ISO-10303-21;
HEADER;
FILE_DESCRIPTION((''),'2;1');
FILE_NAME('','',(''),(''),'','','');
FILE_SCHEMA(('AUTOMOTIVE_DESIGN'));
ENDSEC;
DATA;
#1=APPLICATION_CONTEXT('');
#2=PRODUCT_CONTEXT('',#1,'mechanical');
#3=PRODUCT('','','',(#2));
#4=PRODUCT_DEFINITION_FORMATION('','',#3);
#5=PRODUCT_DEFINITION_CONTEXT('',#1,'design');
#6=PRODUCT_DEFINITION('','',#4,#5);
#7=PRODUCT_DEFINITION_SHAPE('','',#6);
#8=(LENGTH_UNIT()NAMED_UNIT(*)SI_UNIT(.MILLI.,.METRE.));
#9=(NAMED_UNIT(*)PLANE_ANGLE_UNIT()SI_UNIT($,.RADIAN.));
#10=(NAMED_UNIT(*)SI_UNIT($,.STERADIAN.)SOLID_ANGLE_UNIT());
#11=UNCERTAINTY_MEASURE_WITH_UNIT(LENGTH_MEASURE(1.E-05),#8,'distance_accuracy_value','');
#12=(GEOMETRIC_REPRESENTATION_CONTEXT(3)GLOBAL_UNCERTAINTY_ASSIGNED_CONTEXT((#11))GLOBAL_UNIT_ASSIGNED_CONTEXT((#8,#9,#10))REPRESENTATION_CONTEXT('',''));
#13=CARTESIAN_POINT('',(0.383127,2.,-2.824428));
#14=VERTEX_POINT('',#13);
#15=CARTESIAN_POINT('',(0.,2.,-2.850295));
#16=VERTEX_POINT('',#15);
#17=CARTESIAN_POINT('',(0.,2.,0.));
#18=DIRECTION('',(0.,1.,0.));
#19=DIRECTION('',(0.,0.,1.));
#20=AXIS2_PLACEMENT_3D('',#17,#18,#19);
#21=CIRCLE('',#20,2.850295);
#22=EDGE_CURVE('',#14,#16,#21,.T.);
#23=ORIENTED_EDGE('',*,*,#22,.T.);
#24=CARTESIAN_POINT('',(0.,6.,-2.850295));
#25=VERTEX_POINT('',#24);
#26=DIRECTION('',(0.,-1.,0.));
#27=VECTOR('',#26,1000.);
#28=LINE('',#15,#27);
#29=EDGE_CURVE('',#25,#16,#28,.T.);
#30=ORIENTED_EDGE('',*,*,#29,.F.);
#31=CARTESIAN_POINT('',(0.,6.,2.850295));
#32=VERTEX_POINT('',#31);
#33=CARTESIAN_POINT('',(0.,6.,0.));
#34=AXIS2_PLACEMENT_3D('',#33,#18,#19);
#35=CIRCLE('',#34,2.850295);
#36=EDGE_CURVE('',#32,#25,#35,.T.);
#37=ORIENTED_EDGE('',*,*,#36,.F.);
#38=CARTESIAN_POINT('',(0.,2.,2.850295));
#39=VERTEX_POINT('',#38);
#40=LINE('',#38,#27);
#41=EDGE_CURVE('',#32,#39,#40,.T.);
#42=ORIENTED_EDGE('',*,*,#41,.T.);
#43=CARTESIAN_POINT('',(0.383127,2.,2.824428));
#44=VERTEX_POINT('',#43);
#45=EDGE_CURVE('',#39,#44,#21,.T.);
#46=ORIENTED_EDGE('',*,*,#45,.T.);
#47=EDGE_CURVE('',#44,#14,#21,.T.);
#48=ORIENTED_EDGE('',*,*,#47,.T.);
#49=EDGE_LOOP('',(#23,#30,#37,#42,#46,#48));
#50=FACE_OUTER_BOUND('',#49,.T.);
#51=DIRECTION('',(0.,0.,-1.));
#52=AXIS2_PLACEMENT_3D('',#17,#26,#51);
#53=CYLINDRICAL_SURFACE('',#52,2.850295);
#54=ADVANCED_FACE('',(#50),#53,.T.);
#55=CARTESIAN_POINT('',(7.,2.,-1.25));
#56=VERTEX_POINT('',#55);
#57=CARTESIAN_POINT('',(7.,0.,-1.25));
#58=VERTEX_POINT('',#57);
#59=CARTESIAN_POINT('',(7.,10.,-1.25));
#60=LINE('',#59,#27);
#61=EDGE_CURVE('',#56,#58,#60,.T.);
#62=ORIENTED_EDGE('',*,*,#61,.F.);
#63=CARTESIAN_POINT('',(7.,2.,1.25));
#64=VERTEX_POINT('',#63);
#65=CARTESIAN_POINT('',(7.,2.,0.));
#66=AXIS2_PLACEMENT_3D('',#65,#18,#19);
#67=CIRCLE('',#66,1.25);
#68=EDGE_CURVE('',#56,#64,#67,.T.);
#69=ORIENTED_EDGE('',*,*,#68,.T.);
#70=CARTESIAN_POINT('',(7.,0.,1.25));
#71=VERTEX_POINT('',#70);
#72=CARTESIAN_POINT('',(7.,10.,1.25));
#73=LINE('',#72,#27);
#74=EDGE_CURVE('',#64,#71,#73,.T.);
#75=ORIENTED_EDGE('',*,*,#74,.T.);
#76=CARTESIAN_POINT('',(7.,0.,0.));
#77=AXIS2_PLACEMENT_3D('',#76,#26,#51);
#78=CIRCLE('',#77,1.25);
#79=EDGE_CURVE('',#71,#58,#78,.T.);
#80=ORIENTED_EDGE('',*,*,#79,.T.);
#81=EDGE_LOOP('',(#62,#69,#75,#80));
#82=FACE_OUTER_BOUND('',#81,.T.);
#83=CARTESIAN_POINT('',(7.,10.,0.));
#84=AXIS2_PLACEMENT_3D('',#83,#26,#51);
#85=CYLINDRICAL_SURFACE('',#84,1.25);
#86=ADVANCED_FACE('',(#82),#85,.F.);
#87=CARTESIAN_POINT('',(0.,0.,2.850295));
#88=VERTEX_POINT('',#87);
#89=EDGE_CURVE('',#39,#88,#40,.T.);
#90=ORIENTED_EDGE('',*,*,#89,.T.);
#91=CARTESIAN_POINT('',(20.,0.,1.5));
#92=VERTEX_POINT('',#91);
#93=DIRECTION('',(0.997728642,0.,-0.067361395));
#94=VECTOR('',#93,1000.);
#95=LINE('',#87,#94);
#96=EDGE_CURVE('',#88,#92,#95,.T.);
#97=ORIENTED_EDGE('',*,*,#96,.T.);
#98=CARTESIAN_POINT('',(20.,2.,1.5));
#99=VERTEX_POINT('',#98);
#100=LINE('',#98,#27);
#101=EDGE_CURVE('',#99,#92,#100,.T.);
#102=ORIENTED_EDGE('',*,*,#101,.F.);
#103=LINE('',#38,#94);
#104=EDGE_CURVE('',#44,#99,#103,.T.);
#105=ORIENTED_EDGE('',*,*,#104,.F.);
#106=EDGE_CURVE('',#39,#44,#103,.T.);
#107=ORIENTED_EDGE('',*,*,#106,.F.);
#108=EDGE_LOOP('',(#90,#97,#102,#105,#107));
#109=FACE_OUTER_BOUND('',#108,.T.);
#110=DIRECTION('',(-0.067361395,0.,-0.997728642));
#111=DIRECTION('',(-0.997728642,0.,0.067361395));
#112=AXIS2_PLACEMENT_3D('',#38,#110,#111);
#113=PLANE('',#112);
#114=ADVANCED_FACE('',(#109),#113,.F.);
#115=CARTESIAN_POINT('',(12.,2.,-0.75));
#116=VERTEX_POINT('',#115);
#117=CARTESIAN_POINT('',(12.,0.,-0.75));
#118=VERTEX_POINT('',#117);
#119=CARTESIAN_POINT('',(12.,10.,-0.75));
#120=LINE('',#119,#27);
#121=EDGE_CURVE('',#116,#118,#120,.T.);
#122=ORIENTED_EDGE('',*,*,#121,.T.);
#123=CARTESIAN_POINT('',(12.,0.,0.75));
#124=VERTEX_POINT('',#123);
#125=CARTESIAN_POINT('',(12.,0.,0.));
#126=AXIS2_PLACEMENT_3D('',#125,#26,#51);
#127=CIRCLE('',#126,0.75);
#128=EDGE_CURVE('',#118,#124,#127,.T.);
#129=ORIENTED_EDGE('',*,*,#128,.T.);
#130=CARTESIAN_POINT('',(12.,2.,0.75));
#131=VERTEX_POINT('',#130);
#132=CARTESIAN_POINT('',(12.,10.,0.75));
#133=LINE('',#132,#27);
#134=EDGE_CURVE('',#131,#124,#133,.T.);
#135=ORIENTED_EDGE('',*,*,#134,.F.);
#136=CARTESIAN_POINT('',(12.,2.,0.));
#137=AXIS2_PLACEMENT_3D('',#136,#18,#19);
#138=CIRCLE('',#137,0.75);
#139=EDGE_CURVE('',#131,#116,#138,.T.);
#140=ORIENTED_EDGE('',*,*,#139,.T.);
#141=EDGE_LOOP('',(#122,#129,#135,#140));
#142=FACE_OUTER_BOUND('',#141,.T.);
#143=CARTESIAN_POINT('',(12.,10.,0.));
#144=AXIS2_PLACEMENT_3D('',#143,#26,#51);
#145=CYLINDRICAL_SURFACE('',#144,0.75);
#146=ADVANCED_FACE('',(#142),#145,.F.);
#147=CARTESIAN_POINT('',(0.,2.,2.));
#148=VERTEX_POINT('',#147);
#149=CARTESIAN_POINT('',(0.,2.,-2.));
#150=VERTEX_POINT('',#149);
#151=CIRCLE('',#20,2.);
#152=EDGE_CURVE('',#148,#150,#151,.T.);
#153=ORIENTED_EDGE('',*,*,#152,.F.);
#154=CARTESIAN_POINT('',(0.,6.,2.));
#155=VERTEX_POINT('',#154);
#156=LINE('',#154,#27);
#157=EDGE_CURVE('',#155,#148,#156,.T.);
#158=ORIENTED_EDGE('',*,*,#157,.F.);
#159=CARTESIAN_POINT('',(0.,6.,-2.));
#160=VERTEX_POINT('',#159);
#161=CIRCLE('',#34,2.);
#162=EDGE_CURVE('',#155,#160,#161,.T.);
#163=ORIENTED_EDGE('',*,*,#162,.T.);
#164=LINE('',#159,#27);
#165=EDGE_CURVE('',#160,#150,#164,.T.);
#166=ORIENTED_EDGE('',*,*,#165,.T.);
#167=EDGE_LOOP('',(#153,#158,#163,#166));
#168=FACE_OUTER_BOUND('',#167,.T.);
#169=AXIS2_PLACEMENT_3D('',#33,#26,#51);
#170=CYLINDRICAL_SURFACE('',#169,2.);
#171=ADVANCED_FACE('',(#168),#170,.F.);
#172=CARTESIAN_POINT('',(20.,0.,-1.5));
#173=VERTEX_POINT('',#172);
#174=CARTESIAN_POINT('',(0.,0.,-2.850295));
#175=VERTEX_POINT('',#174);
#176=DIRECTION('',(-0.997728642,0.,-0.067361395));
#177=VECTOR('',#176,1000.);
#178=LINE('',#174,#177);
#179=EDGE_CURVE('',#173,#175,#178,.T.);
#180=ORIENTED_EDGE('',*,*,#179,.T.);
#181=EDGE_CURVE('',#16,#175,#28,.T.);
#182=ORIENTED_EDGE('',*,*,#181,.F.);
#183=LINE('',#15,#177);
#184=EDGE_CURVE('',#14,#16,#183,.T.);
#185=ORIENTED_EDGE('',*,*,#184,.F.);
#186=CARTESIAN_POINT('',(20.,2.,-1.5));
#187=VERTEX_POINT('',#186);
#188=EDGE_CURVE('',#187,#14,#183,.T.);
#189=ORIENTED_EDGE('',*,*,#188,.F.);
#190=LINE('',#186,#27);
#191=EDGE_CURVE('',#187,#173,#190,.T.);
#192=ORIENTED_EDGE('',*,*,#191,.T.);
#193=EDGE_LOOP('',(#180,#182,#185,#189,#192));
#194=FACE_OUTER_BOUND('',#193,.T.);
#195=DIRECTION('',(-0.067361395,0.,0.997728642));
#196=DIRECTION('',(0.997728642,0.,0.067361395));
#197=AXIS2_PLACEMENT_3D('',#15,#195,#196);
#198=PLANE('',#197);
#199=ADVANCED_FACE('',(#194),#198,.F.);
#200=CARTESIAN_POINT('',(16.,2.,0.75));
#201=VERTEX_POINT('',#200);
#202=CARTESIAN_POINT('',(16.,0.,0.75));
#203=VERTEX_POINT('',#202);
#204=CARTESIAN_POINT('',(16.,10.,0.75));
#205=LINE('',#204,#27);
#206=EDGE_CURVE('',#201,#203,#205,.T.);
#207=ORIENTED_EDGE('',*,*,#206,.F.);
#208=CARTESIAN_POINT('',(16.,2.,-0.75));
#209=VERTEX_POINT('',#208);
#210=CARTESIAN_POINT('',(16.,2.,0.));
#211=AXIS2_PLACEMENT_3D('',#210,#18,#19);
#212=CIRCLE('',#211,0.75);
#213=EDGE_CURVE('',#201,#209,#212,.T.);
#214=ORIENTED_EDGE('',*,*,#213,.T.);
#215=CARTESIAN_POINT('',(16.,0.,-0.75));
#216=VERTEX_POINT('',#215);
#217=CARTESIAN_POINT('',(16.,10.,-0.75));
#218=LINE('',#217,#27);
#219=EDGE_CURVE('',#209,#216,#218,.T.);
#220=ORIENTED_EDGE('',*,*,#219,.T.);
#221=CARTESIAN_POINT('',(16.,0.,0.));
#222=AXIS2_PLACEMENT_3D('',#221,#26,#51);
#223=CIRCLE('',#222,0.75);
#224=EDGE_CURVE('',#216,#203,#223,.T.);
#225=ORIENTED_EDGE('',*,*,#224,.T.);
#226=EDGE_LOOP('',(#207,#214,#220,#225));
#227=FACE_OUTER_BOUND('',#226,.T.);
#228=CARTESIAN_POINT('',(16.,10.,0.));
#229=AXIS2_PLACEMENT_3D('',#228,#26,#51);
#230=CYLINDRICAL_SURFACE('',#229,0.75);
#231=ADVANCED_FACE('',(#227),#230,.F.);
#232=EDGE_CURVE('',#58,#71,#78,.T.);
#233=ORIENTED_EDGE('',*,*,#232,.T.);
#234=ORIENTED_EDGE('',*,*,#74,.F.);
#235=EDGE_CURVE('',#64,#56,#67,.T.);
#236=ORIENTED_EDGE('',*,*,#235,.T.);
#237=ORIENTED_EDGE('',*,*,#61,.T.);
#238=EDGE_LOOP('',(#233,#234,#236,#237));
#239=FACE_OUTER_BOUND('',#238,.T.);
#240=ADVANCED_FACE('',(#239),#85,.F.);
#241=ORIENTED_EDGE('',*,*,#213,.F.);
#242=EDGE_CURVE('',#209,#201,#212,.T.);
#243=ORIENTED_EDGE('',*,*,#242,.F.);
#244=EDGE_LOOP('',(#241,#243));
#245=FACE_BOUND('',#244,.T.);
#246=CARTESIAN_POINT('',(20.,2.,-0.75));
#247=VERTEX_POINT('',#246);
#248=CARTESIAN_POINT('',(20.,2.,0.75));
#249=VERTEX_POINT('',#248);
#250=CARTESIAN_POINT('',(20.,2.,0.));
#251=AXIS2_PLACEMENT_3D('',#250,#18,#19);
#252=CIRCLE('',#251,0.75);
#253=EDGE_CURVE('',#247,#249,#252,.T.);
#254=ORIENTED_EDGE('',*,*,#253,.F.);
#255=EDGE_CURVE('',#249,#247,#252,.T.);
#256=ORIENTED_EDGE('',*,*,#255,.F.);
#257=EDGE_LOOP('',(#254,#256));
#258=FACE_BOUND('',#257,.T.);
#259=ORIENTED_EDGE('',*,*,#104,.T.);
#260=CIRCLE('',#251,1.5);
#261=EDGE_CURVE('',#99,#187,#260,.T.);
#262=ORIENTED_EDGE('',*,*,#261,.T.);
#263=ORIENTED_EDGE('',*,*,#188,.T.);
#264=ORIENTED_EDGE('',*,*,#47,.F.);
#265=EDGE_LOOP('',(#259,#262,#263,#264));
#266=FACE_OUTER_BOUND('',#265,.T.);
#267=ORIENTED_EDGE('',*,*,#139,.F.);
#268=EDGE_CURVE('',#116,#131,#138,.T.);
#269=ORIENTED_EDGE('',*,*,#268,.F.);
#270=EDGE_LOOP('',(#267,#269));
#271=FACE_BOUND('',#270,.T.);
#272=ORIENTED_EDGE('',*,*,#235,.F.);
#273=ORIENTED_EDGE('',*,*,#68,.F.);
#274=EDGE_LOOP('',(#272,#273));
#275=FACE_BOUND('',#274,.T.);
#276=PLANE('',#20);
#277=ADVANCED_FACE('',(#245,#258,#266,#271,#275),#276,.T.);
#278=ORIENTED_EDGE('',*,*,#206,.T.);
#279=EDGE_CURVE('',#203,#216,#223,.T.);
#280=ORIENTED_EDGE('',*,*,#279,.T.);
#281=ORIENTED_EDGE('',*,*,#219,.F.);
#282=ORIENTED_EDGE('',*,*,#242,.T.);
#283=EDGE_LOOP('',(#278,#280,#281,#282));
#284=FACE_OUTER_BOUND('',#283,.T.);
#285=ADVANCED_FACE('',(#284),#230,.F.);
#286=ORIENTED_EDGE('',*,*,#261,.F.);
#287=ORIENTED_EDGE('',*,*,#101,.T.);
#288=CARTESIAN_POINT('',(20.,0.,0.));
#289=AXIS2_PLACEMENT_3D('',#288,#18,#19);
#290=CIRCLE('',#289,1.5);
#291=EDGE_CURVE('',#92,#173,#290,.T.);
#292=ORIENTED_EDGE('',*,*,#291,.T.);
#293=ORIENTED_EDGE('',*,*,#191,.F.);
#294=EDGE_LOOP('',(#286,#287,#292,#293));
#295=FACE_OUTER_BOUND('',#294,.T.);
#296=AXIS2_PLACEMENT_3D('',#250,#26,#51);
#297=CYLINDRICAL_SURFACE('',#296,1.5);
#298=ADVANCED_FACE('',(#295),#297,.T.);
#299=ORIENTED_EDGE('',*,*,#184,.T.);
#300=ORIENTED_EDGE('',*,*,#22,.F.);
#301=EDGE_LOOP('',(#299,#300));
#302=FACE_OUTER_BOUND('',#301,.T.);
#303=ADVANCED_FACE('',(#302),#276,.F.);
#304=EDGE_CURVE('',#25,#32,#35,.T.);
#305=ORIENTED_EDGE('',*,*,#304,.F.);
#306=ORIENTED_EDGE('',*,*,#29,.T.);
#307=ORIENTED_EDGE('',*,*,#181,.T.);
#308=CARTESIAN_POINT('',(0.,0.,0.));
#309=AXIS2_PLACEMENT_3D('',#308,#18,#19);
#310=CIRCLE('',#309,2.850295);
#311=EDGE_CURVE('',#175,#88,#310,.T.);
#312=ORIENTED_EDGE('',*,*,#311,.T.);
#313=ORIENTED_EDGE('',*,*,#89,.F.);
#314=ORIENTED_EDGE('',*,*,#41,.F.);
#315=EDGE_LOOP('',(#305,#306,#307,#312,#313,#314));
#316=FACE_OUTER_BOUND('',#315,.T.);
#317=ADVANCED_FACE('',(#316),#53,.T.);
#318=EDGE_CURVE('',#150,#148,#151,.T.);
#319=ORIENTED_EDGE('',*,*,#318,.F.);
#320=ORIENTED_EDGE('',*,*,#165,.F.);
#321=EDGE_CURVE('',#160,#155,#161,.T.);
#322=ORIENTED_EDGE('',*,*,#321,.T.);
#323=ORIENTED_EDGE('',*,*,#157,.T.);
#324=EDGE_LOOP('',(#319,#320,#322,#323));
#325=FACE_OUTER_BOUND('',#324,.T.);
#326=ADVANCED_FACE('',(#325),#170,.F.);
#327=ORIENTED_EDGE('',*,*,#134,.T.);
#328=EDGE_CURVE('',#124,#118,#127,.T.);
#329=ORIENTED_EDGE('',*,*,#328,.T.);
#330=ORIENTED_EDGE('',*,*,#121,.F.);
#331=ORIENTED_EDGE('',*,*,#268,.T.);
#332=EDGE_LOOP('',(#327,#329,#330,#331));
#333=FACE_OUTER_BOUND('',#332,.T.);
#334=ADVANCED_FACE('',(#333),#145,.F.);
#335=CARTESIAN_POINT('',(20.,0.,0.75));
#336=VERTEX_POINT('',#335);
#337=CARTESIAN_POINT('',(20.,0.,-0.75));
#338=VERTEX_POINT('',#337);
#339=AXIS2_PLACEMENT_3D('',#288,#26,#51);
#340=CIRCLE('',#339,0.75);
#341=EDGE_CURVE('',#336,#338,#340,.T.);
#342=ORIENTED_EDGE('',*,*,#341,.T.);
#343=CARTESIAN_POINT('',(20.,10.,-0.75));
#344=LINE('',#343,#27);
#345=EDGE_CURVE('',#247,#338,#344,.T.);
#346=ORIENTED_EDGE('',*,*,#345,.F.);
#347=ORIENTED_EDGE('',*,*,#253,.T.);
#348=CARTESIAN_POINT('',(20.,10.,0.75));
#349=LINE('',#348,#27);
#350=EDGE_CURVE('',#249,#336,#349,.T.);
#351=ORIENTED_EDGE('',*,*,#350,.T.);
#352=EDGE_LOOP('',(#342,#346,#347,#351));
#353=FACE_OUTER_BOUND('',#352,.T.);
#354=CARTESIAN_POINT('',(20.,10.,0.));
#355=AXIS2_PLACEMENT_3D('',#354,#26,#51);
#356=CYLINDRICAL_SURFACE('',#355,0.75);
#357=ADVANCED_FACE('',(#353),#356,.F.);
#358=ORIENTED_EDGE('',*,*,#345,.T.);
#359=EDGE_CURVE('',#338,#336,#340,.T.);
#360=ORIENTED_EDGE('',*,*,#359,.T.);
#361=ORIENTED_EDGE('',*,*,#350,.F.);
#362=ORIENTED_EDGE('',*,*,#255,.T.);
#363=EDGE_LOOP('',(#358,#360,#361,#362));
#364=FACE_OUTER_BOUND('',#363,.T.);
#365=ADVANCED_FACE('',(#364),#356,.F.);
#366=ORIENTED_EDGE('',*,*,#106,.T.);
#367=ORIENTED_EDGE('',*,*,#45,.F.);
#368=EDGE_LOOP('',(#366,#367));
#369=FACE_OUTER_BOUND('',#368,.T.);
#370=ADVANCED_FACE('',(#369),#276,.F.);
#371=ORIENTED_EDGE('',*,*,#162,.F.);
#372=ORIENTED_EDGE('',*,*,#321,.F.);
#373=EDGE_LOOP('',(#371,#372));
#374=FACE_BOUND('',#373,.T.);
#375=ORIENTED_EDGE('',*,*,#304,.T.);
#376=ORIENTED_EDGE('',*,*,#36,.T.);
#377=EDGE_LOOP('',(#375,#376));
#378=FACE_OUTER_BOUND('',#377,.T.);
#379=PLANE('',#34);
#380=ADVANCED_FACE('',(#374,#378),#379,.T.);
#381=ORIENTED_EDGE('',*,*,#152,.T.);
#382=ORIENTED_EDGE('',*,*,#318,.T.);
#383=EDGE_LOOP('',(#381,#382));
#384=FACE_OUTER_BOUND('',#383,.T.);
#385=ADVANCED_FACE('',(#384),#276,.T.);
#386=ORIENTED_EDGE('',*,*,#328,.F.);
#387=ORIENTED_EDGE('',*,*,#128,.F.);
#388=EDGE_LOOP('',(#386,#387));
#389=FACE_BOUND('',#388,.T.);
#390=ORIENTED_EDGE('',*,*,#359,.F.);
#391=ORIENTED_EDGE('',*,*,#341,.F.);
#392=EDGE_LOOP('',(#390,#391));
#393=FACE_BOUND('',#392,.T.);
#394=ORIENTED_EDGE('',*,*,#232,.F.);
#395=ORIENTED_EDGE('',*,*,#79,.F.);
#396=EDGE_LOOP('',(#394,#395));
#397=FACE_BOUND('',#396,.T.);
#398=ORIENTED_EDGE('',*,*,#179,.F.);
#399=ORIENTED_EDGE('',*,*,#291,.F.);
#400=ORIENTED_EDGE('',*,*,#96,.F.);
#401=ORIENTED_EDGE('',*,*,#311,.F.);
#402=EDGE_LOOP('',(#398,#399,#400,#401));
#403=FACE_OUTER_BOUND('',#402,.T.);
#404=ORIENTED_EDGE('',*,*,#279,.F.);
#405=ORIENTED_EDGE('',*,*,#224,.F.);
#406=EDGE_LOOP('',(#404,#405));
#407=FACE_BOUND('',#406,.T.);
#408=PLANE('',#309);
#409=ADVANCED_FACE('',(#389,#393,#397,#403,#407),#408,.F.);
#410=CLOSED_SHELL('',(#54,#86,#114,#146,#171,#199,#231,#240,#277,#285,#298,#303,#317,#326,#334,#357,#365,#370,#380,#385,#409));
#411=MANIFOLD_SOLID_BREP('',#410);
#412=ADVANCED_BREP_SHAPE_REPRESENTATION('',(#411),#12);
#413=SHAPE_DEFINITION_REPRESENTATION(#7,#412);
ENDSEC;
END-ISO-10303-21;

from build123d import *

# Parameters (mm, degrees)
BOSS_EXTRUDE1_DEPTH = 2
SKETCH2_R           = 2.85029491
SKETCH2_R_2         = 2
BOSS_EXTRUDE2_DEPTH = 4
SKETCH3_R           = 0.75
SKETCH3_R_2         = 1.25
CUT_EXTRUDE1_DEPTH  = 10


with BuildPart() as part:
    # Sketch1 → Boss-Extrude1 (new body)
    with BuildSketch(Plane(origin=(0, 0, 0), x_dir=(1, 0, 0), z_dir=(0, 1, 0))):
        with BuildLine():
            Line((0, 2.85029491), (20, 1.5))
            ThreePointArc((20, 1.5), (21.5, 0), (20, -1.5))
            Line((20, -1.5), (0, -2.85029491))
            ThreePointArc((0, -2.85029491), (-2.85029491, 0), (0, 2.85029491))
        make_face()
    extrude(amount=BOSS_EXTRUDE1_DEPTH)

    # Sketch2 → Boss-Extrude2 (add)
    with BuildSketch(Plane(origin=(0, 2, 0), x_dir=(1, 0, 0), z_dir=(0, 1, 0))):
        with Locations(Location((0, 0, 0), (0, 0, 270))):
            Circle(SKETCH2_R)
        with Locations(Location((0, 0, 0), (0, 0, 270))):
            Circle(SKETCH2_R_2, mode=Mode.SUBTRACT)
    extrude(amount=BOSS_EXTRUDE2_DEPTH)

    # Sketch3 → Cut-Extrude1 (cut)
    with BuildSketch(Plane.XZ):
        with Locations(Location((16, 0, 0), (0, 0, 270))):
            Circle(SKETCH3_R)
        with Locations(Location((12, 0, 0), (0, 0, 270))):
            Circle(SKETCH3_R)
        with Locations(Location((7, 0, 0), (0, 0, 270))):
            Circle(SKETCH3_R_2)
        with Locations(Location((20, 0, 0), (0, 0, 270))):
            Circle(SKETCH3_R)
    extrude(amount=-CUT_EXTRUDE1_DEPTH, mode=Mode.SUBTRACT)


solid = part.part
